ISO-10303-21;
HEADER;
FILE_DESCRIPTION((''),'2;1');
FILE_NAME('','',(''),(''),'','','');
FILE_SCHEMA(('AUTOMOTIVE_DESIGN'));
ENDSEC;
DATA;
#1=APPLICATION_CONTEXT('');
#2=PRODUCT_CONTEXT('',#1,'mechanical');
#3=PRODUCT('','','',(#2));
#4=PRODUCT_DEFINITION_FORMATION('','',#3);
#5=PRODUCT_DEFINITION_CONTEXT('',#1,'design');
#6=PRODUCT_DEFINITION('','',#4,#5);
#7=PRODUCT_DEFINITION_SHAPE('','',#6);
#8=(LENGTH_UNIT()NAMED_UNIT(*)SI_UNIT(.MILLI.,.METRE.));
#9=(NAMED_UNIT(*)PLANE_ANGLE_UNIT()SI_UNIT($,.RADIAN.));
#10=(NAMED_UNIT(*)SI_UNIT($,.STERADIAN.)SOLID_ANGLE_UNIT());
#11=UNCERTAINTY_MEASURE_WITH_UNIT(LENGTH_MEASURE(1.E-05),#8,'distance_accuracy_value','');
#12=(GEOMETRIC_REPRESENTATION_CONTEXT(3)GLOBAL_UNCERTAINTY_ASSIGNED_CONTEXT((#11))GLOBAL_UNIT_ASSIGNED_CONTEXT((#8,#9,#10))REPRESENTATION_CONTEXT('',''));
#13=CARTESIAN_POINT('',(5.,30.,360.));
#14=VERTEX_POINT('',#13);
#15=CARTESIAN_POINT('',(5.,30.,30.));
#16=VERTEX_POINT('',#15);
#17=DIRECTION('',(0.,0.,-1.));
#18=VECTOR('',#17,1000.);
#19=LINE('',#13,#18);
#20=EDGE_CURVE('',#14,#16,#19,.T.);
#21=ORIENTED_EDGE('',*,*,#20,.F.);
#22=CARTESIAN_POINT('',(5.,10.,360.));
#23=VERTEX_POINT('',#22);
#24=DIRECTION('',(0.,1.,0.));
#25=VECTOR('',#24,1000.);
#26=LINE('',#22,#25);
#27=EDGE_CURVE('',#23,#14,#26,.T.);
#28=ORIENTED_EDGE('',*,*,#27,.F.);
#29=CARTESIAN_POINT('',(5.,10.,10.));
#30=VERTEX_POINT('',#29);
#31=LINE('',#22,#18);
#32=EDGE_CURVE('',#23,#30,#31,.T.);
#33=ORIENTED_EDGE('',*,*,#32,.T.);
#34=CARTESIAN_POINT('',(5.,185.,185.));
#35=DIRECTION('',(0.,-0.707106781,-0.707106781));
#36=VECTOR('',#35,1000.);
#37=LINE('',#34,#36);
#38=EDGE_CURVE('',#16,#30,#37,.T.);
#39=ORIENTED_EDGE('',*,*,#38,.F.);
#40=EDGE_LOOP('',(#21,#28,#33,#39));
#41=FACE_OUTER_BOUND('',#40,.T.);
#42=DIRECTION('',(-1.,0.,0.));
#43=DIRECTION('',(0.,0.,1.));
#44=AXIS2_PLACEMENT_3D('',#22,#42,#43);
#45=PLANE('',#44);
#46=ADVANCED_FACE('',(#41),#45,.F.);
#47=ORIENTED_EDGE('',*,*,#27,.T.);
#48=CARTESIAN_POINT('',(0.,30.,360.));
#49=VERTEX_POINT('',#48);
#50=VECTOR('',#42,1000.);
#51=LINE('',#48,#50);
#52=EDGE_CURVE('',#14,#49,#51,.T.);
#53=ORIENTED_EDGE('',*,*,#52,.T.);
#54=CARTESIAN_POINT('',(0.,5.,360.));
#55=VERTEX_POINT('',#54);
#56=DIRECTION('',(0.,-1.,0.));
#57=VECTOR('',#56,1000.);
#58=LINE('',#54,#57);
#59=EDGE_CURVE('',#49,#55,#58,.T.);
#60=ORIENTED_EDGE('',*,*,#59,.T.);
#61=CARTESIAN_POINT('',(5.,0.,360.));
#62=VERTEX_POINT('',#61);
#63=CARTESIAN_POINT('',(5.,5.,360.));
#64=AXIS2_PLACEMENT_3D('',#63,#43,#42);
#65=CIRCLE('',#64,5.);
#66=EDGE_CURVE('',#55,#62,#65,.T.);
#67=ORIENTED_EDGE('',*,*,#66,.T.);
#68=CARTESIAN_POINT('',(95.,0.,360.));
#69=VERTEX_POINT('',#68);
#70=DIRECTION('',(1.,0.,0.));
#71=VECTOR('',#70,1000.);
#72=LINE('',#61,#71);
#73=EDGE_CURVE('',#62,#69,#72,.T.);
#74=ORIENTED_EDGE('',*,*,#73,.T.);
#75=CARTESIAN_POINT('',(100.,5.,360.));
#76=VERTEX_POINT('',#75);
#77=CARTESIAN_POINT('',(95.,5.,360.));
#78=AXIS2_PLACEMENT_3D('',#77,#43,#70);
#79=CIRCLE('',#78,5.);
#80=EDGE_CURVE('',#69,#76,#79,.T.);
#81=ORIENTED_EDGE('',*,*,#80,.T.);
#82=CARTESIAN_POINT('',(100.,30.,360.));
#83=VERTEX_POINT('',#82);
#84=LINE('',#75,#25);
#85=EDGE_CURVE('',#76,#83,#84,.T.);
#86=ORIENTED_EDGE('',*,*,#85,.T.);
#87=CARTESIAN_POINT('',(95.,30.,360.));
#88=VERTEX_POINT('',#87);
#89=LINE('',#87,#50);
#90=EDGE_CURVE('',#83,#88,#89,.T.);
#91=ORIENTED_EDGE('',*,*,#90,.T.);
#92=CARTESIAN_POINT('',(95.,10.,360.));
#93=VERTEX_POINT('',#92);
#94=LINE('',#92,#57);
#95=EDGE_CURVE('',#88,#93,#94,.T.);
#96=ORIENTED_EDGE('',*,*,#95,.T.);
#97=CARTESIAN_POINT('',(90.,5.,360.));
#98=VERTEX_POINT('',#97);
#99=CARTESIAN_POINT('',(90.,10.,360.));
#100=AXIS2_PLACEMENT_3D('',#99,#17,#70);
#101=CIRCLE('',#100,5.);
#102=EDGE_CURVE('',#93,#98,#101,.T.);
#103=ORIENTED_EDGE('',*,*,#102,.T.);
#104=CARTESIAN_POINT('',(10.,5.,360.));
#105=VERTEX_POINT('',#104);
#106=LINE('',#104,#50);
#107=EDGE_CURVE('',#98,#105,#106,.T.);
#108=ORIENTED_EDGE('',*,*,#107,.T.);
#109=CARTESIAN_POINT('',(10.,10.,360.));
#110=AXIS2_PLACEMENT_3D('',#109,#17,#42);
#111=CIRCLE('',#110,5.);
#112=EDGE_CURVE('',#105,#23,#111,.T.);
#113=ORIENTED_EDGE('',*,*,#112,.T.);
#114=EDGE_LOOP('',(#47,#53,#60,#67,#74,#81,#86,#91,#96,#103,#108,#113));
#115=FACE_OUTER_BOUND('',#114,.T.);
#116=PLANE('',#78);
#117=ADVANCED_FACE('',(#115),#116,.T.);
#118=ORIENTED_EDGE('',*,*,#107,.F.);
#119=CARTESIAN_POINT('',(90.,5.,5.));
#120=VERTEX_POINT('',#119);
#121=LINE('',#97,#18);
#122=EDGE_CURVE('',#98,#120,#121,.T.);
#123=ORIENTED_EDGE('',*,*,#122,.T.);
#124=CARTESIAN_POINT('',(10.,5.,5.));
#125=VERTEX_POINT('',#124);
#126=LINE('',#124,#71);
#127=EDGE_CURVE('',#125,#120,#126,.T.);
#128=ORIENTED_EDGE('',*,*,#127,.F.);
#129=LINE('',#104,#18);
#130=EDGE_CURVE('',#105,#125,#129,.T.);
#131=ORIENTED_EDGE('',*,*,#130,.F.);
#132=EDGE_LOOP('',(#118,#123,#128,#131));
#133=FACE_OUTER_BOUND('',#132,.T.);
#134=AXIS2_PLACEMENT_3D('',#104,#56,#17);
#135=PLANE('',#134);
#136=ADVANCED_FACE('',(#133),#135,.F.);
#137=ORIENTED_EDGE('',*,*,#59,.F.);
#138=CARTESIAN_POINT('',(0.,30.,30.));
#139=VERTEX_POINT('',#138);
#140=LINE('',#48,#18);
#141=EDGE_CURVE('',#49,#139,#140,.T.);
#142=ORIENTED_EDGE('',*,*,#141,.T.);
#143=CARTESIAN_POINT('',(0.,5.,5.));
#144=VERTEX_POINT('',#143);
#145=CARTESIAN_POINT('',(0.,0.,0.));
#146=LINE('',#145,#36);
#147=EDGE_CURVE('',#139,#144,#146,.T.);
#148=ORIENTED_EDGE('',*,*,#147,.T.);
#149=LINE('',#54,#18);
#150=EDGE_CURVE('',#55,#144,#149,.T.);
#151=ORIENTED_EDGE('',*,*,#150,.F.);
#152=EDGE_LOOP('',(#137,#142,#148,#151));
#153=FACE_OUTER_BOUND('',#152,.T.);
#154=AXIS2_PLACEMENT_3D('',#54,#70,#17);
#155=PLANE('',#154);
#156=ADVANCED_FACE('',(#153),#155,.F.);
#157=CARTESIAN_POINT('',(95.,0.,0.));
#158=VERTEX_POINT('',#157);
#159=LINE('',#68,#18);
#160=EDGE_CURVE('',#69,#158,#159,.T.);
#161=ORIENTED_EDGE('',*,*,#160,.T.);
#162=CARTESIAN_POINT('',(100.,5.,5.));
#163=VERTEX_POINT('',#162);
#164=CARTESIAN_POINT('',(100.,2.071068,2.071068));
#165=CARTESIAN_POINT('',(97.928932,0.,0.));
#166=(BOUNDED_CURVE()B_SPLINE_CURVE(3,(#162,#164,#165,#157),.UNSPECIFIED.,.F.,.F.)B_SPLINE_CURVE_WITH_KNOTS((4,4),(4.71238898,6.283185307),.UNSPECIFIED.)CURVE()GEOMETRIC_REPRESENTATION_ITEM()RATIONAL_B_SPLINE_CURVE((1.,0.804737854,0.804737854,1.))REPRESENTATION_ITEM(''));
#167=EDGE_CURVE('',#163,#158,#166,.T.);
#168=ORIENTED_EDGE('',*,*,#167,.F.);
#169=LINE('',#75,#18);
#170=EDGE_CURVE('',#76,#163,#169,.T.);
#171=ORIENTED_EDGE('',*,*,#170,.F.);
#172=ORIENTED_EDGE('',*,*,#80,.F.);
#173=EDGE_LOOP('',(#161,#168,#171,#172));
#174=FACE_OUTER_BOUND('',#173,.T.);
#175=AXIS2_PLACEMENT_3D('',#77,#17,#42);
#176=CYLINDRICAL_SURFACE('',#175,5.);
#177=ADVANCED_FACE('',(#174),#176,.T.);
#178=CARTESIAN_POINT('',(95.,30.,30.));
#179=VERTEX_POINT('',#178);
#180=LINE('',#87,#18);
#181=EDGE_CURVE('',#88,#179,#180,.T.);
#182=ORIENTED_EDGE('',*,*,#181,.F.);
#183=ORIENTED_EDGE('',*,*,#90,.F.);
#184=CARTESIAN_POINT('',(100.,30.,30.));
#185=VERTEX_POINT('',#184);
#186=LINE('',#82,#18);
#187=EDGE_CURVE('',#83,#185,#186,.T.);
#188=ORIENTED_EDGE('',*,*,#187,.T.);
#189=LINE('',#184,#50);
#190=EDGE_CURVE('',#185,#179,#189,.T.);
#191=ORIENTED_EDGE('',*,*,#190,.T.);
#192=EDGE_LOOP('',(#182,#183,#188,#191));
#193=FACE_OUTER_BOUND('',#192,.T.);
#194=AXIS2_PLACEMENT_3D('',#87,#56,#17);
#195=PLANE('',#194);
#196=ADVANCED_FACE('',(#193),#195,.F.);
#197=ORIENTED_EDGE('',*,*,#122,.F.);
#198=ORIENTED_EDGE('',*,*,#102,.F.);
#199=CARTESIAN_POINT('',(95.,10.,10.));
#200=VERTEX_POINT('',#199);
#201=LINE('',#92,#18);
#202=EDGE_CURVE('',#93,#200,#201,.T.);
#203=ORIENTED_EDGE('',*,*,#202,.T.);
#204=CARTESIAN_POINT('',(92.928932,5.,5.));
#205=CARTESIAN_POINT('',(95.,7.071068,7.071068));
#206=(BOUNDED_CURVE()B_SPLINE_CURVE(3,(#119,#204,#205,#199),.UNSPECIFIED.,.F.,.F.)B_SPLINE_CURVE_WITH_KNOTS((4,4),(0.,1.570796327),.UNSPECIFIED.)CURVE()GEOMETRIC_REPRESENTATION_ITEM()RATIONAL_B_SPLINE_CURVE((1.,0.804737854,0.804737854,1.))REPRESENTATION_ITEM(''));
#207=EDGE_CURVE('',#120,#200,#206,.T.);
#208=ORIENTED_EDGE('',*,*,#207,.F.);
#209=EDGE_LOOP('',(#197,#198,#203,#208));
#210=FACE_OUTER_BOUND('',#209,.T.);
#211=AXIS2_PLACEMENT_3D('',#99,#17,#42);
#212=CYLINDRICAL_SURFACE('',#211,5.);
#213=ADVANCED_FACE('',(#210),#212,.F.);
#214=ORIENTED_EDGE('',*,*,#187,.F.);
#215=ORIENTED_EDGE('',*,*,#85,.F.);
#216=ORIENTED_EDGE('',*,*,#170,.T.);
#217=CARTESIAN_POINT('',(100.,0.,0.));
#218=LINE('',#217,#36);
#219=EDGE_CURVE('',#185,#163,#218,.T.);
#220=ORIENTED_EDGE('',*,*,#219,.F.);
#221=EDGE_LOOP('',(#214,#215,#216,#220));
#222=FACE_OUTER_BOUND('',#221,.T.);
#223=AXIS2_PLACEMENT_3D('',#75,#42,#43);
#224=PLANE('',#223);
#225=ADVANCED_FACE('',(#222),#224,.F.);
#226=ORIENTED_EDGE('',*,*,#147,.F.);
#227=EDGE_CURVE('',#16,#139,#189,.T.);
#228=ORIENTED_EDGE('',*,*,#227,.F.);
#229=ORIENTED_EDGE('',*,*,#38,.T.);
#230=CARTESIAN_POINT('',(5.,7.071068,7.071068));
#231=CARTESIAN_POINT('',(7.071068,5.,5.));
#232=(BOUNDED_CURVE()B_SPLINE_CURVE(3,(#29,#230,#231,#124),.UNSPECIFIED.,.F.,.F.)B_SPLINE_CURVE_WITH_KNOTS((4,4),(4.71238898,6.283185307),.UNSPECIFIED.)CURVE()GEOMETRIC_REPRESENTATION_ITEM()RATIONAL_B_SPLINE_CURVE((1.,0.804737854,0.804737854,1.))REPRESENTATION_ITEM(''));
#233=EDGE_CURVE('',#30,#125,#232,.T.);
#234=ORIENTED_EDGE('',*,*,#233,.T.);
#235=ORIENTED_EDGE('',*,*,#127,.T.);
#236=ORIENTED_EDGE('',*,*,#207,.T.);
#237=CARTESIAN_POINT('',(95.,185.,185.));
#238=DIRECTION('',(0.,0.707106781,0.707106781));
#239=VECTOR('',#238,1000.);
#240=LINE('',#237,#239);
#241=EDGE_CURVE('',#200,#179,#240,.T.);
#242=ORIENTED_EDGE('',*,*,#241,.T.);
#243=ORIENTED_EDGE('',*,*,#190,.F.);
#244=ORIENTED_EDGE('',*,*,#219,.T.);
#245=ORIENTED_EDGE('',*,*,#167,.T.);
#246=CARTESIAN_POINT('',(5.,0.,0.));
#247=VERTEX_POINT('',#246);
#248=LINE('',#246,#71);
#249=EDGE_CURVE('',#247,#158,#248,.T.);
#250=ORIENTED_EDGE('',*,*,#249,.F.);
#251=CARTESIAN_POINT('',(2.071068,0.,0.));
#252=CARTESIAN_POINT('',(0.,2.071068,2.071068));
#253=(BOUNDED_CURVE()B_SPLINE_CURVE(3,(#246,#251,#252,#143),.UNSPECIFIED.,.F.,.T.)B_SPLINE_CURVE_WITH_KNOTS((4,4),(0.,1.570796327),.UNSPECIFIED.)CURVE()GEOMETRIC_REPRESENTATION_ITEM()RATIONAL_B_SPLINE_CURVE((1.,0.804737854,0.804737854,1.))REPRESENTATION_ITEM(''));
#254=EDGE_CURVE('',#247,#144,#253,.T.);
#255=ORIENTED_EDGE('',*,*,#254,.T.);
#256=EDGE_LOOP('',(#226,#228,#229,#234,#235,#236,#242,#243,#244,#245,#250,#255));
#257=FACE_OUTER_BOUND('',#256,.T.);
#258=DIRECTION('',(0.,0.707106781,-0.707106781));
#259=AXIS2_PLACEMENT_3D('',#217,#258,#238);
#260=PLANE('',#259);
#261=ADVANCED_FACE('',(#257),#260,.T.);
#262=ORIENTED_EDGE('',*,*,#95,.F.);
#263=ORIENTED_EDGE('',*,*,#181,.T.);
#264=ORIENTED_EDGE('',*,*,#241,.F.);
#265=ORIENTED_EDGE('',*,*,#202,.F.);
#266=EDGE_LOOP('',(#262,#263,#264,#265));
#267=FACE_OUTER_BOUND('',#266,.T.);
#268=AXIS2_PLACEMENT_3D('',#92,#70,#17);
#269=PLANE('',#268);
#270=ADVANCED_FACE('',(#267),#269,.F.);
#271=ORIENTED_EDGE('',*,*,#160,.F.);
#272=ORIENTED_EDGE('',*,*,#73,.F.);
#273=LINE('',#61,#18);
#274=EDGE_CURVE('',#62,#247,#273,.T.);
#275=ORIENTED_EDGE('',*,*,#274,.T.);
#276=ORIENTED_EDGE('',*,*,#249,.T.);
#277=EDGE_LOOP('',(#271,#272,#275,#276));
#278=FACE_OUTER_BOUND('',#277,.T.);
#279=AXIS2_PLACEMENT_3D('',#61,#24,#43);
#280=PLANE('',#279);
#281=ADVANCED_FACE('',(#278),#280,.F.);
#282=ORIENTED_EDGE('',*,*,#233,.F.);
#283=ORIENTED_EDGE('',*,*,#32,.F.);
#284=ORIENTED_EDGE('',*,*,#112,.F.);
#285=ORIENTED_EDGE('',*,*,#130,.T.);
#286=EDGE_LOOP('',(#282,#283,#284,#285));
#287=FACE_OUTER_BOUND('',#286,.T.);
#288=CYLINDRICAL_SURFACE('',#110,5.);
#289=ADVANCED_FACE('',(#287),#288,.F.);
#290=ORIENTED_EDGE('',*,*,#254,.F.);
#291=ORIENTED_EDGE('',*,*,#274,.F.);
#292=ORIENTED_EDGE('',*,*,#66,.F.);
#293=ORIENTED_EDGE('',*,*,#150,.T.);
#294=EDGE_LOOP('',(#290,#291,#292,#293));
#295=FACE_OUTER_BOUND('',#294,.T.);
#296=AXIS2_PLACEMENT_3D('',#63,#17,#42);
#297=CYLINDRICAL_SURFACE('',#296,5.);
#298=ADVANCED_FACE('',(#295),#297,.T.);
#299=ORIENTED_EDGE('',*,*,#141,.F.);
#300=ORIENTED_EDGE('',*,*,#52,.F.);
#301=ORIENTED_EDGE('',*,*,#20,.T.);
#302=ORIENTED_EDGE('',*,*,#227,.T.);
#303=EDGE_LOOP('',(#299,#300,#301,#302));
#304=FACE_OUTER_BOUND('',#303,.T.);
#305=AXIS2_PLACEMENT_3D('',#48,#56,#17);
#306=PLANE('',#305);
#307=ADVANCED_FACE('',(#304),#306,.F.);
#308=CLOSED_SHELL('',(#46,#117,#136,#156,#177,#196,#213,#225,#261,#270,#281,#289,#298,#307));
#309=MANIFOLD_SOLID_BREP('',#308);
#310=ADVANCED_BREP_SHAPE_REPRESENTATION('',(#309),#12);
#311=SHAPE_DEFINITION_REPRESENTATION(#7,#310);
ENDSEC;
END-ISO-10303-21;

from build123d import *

# Parameters (mm, degrees)
EXTRUDE_1_DEPTH     = 360
CUT_EXTRUDE_1_DEPTH = 375.83329628


with BuildPart() as part:
    # 草图1 → 凸台-拉伸1 (new body)
    with BuildSketch(Plane.XY):
        with BuildLine():
            Line((5, 0), (95, 0))
            ThreePointArc((95, 0), (98.535533906, 1.464466094), (100, 5))
            Line((100, 5), (100, 30))
            Line((100, 30), (95, 30))
            Line((95, 30), (95, 10))
            ThreePointArc((95, 10), (93.535533906, 6.464466094), (90, 5))
            Line((90, 5), (10, 5))
            ThreePointArc((10, 5), (6.464466094, 6.464466094), (5, 10))
            Line((5, 10), (5, 30))
            Line((5, 30), (0, 30))
            Line((0, 30), (0, 5))
            ThreePointArc((0, 5), (1.464466094, 1.464466094), (5, 0))
        make_face()
    extrude(amount=EXTRUDE_1_DEPTH)

    # 草图2 → 切除-拉伸1 (cut, through all)
    with BuildSketch(Plane.ZY):
        Polygon((5, 5), (30, 30), (0, 30), (0, 5), align=None)
        Polygon((0, 0), (5, 5), (0, 5), align=None)
    extrude(amount=-CUT_EXTRUDE_1_DEPTH, mode=Mode.SUBTRACT)


solid = part.part
